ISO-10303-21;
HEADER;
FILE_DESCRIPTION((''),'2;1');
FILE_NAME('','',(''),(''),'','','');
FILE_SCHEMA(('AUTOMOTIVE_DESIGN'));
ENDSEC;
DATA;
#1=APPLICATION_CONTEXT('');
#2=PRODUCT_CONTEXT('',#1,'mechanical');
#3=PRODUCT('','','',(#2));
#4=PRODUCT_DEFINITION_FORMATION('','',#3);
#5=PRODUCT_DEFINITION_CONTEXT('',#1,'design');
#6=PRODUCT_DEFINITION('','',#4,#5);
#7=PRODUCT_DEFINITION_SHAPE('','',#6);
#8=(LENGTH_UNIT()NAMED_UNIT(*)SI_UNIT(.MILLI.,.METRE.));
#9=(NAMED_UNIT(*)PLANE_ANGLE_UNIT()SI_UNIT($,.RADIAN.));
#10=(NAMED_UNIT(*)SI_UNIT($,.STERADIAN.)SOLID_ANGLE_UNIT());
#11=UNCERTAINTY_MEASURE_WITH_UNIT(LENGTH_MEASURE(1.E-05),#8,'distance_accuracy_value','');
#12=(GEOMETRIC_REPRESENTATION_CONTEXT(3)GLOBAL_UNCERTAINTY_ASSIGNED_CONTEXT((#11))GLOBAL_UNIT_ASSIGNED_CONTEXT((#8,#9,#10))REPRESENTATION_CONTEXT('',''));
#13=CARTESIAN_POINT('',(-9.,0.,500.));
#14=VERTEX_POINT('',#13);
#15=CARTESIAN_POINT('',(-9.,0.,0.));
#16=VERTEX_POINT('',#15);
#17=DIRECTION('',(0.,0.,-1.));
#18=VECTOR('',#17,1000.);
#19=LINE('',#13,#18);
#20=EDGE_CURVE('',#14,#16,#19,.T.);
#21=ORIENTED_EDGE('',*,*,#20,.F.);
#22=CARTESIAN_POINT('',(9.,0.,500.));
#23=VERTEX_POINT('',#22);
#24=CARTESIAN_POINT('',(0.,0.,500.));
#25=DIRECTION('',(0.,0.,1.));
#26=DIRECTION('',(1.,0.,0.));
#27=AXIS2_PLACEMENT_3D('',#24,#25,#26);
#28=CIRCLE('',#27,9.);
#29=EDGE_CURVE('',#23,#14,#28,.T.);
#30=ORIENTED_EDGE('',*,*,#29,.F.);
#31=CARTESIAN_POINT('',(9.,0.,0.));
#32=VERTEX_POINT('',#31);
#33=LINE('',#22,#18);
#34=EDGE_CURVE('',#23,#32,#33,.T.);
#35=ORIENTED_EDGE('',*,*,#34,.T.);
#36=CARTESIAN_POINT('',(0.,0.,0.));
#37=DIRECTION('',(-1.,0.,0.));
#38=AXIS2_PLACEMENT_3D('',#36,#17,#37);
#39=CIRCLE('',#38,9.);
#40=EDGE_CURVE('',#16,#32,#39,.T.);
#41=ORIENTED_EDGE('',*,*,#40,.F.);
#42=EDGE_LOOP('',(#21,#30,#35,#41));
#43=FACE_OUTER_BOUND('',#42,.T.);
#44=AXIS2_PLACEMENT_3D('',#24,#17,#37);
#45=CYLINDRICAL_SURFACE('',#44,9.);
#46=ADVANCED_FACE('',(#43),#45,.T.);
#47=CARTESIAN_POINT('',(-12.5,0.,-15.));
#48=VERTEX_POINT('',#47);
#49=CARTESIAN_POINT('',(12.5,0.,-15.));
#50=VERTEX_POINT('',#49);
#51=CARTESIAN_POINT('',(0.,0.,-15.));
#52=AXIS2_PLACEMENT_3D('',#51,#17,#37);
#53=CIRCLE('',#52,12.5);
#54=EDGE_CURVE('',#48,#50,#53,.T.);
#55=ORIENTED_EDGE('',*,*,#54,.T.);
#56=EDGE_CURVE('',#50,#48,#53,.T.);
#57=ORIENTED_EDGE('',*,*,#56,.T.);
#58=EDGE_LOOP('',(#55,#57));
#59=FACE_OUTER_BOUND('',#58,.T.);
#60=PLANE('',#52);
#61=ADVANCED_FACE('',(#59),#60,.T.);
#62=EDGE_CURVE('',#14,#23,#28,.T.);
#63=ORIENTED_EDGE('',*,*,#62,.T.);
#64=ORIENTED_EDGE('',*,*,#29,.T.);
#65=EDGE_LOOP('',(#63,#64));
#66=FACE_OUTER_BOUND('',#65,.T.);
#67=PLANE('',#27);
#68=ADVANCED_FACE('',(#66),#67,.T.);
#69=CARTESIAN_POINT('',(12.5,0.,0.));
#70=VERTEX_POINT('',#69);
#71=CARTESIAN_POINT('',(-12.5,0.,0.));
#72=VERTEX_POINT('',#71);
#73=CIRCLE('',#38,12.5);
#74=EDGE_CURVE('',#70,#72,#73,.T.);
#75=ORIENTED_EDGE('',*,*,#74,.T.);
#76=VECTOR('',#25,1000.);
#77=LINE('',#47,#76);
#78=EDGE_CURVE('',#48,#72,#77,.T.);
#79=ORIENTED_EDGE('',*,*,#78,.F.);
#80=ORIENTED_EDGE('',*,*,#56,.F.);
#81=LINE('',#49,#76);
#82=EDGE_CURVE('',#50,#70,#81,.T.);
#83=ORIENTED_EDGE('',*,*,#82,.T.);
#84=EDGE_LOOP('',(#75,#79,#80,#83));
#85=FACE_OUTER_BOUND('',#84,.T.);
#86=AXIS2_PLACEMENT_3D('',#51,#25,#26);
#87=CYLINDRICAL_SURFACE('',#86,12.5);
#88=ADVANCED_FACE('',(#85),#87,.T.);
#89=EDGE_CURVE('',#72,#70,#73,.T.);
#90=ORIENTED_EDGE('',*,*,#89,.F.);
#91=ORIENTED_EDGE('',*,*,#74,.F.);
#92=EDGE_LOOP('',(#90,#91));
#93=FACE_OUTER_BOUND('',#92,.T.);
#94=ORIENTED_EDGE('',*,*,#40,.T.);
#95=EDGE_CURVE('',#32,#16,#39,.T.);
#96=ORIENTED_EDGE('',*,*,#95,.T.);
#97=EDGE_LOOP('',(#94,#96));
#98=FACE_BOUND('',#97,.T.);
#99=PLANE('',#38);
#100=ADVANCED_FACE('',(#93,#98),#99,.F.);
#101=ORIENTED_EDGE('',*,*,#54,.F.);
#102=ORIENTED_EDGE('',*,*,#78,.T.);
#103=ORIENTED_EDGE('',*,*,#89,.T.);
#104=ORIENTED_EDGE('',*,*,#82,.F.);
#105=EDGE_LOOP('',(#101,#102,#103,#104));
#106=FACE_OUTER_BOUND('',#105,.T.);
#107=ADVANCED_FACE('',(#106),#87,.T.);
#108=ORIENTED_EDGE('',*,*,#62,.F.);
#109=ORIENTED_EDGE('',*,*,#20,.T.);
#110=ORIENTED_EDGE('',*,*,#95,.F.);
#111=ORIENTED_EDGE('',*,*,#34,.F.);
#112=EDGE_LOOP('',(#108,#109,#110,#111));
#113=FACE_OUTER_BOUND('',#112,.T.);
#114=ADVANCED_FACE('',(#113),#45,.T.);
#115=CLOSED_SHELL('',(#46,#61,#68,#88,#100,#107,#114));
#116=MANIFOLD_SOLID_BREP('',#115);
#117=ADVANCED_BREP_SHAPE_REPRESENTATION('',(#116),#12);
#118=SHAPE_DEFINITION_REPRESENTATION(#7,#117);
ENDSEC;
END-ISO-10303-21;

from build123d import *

# Parameters (mm, degrees)
SKETCH1_R           = 9
BOSS_EXTRUDE1_DEPTH = 500
SKETCH2_R           = 12.5
BOSS_EXTRUDE2_DEPTH = 15


with BuildPart() as part:
    # Sketch1 → Boss-Extrude1 (new body)
    with BuildSketch(Plane.XY):
        Circle(SKETCH1_R)
    extrude(amount=BOSS_EXTRUDE1_DEPTH)

    # Sketch2 → Boss-Extrude2 (add)
    with BuildSketch(Plane(origin=(0, 0, 0), x_dir=(-1, 0, 0), z_dir=(0, 0, -1))):
        Circle(SKETCH2_R)
    extrude(amount=BOSS_EXTRUDE2_DEPTH)


solid = part.part
